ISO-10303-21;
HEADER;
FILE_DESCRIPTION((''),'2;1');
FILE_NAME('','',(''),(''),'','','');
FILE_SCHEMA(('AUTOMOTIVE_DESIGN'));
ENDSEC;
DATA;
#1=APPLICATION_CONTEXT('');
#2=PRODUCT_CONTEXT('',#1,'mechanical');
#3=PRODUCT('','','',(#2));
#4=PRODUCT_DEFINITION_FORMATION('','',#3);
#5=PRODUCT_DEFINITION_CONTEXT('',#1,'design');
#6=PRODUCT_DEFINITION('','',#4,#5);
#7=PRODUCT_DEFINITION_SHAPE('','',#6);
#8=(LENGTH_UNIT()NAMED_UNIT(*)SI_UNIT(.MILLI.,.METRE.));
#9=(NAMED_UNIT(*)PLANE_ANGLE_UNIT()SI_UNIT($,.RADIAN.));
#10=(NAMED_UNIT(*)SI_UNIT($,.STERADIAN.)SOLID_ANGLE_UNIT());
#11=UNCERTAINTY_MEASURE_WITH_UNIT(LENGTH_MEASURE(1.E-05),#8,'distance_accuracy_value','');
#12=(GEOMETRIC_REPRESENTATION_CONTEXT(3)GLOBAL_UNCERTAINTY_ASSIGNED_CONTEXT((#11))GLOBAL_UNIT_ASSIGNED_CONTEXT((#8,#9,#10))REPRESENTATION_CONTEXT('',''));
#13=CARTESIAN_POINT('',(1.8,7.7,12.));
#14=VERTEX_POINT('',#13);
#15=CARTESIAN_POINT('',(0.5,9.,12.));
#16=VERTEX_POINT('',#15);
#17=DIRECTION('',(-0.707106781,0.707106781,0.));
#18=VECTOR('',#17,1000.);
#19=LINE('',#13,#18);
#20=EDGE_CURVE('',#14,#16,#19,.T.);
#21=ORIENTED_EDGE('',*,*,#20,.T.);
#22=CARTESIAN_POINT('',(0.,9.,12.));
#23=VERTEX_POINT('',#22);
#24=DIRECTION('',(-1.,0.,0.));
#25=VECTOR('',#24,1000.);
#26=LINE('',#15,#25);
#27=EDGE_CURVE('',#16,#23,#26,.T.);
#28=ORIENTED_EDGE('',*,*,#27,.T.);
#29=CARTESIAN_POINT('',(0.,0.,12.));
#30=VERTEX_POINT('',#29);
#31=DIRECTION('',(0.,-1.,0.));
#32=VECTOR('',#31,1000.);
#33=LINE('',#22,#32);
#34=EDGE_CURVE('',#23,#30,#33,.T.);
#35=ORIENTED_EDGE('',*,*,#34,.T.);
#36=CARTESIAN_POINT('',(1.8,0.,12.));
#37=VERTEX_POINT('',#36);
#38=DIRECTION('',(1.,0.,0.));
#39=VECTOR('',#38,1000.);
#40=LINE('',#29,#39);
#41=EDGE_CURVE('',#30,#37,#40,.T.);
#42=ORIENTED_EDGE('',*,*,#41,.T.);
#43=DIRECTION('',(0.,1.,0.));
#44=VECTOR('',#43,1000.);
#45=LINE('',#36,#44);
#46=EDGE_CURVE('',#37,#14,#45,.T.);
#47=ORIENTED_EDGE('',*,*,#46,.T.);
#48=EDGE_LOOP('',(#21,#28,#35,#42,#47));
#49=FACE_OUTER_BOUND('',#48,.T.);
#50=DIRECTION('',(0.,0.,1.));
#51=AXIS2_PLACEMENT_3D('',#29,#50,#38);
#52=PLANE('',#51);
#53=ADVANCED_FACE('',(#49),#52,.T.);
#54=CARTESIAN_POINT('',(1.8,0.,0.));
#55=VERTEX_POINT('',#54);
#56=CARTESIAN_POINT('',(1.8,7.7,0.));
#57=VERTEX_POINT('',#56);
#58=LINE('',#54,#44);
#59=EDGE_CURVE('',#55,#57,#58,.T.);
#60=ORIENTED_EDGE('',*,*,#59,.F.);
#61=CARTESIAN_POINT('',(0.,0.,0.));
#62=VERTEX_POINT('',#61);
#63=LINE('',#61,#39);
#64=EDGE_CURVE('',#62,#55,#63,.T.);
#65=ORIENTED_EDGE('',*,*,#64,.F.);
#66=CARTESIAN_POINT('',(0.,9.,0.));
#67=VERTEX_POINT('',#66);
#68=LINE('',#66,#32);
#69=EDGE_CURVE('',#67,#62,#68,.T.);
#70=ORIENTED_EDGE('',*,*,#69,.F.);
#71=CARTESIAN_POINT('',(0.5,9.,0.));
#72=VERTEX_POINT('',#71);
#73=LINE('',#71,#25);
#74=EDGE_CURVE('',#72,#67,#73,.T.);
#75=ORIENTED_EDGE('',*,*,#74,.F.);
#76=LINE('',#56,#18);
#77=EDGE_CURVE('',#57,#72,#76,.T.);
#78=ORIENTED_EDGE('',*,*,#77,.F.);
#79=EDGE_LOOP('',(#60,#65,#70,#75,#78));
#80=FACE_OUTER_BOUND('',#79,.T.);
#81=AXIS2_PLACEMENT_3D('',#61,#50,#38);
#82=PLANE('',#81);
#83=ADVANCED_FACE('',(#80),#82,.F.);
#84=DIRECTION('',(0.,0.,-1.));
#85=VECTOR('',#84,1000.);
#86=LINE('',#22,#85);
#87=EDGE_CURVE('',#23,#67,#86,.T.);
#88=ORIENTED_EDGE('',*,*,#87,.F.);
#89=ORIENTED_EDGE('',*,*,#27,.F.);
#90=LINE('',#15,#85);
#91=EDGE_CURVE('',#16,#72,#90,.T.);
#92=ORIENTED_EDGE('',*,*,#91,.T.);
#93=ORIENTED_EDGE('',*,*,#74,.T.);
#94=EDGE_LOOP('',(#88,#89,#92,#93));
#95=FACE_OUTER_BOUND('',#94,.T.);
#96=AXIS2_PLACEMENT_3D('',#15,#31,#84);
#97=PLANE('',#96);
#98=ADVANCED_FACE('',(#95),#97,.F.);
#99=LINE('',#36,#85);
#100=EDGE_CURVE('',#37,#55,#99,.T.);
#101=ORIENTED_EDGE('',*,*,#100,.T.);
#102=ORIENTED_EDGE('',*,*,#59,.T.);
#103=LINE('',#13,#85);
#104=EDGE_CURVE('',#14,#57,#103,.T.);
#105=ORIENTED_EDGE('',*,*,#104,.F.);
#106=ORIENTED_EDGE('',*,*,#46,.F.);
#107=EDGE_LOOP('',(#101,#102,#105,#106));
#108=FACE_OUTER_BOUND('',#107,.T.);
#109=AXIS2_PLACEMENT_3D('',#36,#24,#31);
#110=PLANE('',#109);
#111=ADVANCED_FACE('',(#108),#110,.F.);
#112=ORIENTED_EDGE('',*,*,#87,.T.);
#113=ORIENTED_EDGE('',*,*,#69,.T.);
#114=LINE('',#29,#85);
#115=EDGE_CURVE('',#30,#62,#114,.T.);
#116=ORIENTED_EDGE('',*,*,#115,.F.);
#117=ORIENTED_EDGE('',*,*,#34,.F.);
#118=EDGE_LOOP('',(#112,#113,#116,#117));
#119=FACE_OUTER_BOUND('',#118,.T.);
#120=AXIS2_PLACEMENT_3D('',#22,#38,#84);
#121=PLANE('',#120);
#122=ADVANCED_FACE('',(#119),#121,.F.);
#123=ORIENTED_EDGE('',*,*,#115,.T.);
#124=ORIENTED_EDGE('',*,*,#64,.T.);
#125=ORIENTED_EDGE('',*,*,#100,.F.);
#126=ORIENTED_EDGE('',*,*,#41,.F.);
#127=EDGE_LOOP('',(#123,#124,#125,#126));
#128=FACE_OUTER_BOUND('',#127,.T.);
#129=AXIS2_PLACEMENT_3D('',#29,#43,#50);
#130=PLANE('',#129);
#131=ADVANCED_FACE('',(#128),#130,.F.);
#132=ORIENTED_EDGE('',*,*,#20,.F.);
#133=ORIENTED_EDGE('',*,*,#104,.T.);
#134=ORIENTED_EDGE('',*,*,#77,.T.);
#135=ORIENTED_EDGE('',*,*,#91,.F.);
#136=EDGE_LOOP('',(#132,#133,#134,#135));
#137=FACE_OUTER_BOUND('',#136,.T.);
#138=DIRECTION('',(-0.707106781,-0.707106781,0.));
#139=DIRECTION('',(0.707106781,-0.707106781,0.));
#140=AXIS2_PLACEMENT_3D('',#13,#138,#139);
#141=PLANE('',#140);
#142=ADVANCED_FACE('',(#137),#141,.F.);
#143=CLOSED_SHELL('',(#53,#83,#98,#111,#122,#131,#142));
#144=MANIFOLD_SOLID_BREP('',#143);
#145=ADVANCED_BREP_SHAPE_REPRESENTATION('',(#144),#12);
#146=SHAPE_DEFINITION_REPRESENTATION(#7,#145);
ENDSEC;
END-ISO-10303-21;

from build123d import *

# Parameters (mm, degrees)
EXTRUDE_1_DEPTH = 12


with BuildPart() as part:
    # 草图1 → 凸台-拉伸1 (new body)
    with BuildSketch(Plane.XY):
        Polygon((0, 9), (0, 0), (1.8, 0), (1.8, 7.7), (0.5, 9), align=None)
    extrude(amount=EXTRUDE_1_DEPTH)


solid = part.part
